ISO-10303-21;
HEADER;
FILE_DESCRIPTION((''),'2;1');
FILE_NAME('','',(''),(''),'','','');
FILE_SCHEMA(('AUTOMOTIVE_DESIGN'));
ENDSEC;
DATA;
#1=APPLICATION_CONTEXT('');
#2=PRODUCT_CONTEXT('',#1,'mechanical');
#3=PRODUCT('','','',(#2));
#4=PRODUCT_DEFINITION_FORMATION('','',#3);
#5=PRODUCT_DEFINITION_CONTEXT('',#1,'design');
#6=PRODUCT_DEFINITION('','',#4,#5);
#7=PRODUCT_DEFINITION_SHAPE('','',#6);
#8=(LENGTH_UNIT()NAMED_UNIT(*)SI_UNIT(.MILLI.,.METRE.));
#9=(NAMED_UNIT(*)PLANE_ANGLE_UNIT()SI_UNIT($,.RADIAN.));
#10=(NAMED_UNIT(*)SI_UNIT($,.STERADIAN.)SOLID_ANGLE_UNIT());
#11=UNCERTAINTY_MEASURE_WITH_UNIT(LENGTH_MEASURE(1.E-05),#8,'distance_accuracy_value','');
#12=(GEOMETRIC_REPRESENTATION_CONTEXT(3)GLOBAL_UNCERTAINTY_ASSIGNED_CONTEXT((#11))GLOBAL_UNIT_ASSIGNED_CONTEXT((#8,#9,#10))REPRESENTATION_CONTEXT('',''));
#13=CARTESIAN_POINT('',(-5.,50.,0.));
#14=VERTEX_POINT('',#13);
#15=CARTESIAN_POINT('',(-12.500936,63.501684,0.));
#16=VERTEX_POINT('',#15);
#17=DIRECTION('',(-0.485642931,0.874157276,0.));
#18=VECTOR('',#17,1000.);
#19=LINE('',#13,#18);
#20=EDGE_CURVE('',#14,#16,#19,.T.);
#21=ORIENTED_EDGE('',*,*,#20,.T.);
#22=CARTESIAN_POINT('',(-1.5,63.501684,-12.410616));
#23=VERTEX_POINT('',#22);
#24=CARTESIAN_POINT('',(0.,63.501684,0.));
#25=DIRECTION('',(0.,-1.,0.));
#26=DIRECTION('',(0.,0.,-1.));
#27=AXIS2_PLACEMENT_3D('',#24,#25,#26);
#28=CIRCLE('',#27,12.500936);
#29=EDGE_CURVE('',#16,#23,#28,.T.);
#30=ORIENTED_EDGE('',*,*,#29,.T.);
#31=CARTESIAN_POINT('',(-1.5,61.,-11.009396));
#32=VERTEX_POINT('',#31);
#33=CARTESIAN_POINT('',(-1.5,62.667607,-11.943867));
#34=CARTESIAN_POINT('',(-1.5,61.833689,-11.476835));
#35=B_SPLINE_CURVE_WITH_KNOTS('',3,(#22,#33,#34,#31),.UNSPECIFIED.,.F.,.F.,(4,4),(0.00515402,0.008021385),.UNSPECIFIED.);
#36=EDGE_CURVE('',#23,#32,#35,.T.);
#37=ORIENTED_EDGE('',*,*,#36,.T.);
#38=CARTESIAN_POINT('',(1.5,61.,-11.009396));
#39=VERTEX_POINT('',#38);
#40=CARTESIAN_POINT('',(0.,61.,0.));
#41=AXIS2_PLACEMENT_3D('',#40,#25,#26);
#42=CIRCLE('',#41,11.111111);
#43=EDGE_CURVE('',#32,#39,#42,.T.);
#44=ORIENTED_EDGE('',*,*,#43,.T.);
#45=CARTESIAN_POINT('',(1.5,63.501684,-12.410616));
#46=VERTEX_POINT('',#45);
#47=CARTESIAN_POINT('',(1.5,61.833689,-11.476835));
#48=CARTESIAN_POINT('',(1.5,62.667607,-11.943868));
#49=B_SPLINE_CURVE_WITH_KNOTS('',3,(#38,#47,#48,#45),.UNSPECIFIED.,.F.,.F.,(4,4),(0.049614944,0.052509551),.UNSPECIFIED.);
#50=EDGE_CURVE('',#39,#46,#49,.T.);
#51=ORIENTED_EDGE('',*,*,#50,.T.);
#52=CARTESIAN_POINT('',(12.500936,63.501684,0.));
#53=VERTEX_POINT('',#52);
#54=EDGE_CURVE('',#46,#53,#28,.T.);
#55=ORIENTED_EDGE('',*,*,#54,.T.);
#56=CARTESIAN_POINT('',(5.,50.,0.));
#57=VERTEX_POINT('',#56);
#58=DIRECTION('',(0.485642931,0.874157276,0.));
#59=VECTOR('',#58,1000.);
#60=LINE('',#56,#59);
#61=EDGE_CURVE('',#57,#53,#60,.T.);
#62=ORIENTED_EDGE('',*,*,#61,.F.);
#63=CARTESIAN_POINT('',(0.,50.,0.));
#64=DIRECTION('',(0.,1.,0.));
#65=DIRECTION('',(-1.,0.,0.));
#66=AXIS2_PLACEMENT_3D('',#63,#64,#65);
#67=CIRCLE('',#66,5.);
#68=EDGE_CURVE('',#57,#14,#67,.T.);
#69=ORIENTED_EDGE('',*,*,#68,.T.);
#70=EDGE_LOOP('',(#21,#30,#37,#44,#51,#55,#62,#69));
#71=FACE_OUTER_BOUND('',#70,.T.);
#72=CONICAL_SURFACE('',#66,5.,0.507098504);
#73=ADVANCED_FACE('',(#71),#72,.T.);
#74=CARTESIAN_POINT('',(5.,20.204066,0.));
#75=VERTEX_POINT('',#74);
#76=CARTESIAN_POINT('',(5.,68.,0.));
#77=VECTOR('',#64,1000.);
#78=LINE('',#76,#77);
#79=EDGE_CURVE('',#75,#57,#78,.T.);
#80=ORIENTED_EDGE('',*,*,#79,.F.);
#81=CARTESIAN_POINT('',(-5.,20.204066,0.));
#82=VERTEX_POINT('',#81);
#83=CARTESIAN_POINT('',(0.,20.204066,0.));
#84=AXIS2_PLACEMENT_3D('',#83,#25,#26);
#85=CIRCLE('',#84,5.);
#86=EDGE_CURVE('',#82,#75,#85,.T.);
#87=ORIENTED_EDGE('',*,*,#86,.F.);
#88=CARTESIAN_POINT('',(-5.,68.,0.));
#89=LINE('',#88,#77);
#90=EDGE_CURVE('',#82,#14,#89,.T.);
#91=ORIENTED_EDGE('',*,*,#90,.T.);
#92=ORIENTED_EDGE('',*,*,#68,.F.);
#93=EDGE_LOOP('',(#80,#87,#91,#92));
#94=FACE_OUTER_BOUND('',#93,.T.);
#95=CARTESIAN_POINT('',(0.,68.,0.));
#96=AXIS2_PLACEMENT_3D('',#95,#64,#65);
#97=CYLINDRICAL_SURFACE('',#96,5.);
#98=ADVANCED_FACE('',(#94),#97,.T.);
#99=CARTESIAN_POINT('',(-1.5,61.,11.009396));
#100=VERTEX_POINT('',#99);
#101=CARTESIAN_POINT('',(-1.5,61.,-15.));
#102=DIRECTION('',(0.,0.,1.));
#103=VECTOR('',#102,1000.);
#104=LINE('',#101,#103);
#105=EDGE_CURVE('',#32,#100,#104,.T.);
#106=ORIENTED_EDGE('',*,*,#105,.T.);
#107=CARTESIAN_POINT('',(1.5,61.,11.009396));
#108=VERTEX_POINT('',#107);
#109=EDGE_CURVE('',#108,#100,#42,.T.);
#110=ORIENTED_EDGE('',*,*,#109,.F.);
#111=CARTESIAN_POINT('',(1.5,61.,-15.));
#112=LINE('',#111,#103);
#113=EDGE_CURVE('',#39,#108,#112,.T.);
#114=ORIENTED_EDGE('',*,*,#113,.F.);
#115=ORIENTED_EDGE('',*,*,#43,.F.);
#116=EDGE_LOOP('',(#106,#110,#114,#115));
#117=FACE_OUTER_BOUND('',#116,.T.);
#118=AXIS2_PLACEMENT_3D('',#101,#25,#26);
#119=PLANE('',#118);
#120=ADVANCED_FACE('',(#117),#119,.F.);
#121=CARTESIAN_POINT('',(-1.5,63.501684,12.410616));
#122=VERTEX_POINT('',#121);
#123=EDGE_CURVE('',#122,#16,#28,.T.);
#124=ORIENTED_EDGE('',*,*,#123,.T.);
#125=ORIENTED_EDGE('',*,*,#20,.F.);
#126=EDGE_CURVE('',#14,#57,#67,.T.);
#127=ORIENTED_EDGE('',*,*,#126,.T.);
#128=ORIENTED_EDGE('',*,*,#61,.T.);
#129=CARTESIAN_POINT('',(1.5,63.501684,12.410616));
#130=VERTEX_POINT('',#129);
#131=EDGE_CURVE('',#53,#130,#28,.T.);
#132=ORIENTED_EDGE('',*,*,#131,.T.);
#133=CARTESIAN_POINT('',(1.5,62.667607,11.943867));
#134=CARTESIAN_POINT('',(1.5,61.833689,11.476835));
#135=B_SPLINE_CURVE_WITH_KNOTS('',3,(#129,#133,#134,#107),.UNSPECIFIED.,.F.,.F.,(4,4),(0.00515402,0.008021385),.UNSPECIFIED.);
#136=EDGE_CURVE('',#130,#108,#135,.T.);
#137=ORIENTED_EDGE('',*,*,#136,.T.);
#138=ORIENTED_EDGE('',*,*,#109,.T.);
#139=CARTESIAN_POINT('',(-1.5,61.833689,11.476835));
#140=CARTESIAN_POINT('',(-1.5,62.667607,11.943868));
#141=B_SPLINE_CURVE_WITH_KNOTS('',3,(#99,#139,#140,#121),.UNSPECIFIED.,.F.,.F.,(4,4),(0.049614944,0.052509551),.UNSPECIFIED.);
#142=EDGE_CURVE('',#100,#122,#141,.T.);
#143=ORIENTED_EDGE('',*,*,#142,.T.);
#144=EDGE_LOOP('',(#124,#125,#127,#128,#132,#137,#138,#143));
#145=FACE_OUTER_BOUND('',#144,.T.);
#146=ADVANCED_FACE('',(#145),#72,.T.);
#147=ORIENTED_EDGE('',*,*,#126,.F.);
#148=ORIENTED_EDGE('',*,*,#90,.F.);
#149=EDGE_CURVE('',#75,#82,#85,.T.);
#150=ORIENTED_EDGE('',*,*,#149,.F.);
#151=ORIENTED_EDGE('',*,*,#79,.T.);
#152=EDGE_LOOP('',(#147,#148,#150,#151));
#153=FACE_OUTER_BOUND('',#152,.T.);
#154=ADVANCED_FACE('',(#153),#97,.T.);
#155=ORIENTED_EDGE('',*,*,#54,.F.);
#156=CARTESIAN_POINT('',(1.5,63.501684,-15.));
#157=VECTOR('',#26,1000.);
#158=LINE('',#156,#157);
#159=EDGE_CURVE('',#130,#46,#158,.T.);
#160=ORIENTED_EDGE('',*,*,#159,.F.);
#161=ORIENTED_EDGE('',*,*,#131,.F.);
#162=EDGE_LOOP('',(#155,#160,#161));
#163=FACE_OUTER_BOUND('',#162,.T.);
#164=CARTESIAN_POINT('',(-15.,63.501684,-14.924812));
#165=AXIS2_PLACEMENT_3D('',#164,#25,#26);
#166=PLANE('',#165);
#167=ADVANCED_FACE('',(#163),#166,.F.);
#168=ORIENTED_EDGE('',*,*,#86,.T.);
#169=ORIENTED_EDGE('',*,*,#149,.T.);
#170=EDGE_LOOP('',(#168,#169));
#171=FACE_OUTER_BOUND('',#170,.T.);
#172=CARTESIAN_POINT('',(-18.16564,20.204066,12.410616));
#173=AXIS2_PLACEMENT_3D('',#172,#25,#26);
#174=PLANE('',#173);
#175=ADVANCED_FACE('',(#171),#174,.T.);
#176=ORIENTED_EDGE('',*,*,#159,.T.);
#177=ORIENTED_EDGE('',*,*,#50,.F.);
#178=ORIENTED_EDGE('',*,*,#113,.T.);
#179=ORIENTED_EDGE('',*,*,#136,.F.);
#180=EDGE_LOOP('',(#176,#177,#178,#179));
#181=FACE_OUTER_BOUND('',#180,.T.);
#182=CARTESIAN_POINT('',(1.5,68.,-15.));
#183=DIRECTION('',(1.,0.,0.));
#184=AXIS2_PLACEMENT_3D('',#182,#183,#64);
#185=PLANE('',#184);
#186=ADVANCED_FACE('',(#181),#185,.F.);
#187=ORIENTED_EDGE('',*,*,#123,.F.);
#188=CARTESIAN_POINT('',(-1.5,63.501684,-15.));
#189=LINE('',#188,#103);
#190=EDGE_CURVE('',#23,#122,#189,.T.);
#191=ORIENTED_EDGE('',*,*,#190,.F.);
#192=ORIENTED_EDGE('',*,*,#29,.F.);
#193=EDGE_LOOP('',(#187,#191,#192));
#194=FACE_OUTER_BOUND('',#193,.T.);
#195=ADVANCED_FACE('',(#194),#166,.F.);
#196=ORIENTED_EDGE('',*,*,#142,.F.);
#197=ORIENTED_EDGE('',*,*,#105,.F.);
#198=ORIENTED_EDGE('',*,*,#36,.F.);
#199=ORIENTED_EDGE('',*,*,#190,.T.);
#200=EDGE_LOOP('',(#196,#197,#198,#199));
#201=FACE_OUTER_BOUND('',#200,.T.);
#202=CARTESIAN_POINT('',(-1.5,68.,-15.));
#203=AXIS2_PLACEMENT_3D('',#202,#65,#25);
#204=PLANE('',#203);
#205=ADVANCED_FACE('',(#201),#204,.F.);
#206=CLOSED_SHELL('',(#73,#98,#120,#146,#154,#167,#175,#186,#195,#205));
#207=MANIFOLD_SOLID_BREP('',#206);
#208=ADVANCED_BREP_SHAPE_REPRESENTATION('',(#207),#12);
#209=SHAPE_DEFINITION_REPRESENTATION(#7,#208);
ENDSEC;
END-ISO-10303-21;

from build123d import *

# Parameters (mm, degrees)
HEAD_SLOT_CUT_DEPTH      = 72.232015274
HEAD_SLOT_CUT_DEPTH_BACK = 72.232015274
HEAD_SLOT_SKETCH_W       = 3
HEAD_SLOT_SKETCH_H       = 7
TRIM_CUT_1_DEPTH         = 72.216220063
TRIM_CUT_1_DEPTH_BACK    = 72.216220063
TRIM_CUT_1_SKETCH_W      = 30.281079354
TRIM_CUT_1_SKETCH_H      = 4.498315547
TRIM_CUT_2_DEPTH         = 66.899626103
TRIM_CUT_2_DEPTH_BACK    = 66.899626103
TRIM_CUT_2_SKETCH_W      = 29.08434912
TRIM_CUT_2_SKETCH_H      = 20.204065749


with BuildPart() as part:
    # Screw Half Profile Sketch → Screw Body Revolve (revolve)
    with BuildSketch(Plane.XY, mode=Mode.PRIVATE) as screw_body_revolve_sk:
        Polygon((0, 0), (5, 0), (5, 50), (15, 68), (0, 68), align=None)
    revolve(screw_body_revolve_sk.sketch.rotate(Axis((0, 68, 0), (0, -1, 0)), 180), axis=Axis((0, 68, 0), (0, -1, 0)))

    # Head Slot Sketch → Head Slot Cut (cut, two sides: drawn at the far end of the back side and taken through both)
    with BuildSketch(Plane.XY.offset(-HEAD_SLOT_CUT_DEPTH_BACK)):
        with Locations((0, 64.5)):
            Rectangle(HEAD_SLOT_SKETCH_W, HEAD_SLOT_SKETCH_H)
    extrude(amount=HEAD_SLOT_CUT_DEPTH + HEAD_SLOT_CUT_DEPTH_BACK, mode=Mode.SUBTRACT)

    # Trim Cut 1 Sketch → Trim Cut 1 (cut, two sides: drawn at the far end of the back side and taken through both)
    with BuildSketch(Plane.XY.offset(-TRIM_CUT_1_DEPTH_BACK)):
        with Locations((0.140539677, 65.750842226)):
            Rectangle(TRIM_CUT_1_SKETCH_W, TRIM_CUT_1_SKETCH_H)
    extrude(amount=TRIM_CUT_1_DEPTH + TRIM_CUT_1_DEPTH_BACK, mode=Mode.SUBTRACT)

    # Trim Cut 2 Sketch → Trim Cut 2 (cut, two sides: drawn at the far end of the back side and taken through both)
    with BuildSketch(Plane.XY.offset(-TRIM_CUT_2_DEPTH_BACK)):
        with Locations((-3.623465422, 10.102032875)):
            Rectangle(TRIM_CUT_2_SKETCH_W, TRIM_CUT_2_SKETCH_H)
    extrude(amount=TRIM_CUT_2_DEPTH + TRIM_CUT_2_DEPTH_BACK, mode=Mode.SUBTRACT)


solid = part.part
